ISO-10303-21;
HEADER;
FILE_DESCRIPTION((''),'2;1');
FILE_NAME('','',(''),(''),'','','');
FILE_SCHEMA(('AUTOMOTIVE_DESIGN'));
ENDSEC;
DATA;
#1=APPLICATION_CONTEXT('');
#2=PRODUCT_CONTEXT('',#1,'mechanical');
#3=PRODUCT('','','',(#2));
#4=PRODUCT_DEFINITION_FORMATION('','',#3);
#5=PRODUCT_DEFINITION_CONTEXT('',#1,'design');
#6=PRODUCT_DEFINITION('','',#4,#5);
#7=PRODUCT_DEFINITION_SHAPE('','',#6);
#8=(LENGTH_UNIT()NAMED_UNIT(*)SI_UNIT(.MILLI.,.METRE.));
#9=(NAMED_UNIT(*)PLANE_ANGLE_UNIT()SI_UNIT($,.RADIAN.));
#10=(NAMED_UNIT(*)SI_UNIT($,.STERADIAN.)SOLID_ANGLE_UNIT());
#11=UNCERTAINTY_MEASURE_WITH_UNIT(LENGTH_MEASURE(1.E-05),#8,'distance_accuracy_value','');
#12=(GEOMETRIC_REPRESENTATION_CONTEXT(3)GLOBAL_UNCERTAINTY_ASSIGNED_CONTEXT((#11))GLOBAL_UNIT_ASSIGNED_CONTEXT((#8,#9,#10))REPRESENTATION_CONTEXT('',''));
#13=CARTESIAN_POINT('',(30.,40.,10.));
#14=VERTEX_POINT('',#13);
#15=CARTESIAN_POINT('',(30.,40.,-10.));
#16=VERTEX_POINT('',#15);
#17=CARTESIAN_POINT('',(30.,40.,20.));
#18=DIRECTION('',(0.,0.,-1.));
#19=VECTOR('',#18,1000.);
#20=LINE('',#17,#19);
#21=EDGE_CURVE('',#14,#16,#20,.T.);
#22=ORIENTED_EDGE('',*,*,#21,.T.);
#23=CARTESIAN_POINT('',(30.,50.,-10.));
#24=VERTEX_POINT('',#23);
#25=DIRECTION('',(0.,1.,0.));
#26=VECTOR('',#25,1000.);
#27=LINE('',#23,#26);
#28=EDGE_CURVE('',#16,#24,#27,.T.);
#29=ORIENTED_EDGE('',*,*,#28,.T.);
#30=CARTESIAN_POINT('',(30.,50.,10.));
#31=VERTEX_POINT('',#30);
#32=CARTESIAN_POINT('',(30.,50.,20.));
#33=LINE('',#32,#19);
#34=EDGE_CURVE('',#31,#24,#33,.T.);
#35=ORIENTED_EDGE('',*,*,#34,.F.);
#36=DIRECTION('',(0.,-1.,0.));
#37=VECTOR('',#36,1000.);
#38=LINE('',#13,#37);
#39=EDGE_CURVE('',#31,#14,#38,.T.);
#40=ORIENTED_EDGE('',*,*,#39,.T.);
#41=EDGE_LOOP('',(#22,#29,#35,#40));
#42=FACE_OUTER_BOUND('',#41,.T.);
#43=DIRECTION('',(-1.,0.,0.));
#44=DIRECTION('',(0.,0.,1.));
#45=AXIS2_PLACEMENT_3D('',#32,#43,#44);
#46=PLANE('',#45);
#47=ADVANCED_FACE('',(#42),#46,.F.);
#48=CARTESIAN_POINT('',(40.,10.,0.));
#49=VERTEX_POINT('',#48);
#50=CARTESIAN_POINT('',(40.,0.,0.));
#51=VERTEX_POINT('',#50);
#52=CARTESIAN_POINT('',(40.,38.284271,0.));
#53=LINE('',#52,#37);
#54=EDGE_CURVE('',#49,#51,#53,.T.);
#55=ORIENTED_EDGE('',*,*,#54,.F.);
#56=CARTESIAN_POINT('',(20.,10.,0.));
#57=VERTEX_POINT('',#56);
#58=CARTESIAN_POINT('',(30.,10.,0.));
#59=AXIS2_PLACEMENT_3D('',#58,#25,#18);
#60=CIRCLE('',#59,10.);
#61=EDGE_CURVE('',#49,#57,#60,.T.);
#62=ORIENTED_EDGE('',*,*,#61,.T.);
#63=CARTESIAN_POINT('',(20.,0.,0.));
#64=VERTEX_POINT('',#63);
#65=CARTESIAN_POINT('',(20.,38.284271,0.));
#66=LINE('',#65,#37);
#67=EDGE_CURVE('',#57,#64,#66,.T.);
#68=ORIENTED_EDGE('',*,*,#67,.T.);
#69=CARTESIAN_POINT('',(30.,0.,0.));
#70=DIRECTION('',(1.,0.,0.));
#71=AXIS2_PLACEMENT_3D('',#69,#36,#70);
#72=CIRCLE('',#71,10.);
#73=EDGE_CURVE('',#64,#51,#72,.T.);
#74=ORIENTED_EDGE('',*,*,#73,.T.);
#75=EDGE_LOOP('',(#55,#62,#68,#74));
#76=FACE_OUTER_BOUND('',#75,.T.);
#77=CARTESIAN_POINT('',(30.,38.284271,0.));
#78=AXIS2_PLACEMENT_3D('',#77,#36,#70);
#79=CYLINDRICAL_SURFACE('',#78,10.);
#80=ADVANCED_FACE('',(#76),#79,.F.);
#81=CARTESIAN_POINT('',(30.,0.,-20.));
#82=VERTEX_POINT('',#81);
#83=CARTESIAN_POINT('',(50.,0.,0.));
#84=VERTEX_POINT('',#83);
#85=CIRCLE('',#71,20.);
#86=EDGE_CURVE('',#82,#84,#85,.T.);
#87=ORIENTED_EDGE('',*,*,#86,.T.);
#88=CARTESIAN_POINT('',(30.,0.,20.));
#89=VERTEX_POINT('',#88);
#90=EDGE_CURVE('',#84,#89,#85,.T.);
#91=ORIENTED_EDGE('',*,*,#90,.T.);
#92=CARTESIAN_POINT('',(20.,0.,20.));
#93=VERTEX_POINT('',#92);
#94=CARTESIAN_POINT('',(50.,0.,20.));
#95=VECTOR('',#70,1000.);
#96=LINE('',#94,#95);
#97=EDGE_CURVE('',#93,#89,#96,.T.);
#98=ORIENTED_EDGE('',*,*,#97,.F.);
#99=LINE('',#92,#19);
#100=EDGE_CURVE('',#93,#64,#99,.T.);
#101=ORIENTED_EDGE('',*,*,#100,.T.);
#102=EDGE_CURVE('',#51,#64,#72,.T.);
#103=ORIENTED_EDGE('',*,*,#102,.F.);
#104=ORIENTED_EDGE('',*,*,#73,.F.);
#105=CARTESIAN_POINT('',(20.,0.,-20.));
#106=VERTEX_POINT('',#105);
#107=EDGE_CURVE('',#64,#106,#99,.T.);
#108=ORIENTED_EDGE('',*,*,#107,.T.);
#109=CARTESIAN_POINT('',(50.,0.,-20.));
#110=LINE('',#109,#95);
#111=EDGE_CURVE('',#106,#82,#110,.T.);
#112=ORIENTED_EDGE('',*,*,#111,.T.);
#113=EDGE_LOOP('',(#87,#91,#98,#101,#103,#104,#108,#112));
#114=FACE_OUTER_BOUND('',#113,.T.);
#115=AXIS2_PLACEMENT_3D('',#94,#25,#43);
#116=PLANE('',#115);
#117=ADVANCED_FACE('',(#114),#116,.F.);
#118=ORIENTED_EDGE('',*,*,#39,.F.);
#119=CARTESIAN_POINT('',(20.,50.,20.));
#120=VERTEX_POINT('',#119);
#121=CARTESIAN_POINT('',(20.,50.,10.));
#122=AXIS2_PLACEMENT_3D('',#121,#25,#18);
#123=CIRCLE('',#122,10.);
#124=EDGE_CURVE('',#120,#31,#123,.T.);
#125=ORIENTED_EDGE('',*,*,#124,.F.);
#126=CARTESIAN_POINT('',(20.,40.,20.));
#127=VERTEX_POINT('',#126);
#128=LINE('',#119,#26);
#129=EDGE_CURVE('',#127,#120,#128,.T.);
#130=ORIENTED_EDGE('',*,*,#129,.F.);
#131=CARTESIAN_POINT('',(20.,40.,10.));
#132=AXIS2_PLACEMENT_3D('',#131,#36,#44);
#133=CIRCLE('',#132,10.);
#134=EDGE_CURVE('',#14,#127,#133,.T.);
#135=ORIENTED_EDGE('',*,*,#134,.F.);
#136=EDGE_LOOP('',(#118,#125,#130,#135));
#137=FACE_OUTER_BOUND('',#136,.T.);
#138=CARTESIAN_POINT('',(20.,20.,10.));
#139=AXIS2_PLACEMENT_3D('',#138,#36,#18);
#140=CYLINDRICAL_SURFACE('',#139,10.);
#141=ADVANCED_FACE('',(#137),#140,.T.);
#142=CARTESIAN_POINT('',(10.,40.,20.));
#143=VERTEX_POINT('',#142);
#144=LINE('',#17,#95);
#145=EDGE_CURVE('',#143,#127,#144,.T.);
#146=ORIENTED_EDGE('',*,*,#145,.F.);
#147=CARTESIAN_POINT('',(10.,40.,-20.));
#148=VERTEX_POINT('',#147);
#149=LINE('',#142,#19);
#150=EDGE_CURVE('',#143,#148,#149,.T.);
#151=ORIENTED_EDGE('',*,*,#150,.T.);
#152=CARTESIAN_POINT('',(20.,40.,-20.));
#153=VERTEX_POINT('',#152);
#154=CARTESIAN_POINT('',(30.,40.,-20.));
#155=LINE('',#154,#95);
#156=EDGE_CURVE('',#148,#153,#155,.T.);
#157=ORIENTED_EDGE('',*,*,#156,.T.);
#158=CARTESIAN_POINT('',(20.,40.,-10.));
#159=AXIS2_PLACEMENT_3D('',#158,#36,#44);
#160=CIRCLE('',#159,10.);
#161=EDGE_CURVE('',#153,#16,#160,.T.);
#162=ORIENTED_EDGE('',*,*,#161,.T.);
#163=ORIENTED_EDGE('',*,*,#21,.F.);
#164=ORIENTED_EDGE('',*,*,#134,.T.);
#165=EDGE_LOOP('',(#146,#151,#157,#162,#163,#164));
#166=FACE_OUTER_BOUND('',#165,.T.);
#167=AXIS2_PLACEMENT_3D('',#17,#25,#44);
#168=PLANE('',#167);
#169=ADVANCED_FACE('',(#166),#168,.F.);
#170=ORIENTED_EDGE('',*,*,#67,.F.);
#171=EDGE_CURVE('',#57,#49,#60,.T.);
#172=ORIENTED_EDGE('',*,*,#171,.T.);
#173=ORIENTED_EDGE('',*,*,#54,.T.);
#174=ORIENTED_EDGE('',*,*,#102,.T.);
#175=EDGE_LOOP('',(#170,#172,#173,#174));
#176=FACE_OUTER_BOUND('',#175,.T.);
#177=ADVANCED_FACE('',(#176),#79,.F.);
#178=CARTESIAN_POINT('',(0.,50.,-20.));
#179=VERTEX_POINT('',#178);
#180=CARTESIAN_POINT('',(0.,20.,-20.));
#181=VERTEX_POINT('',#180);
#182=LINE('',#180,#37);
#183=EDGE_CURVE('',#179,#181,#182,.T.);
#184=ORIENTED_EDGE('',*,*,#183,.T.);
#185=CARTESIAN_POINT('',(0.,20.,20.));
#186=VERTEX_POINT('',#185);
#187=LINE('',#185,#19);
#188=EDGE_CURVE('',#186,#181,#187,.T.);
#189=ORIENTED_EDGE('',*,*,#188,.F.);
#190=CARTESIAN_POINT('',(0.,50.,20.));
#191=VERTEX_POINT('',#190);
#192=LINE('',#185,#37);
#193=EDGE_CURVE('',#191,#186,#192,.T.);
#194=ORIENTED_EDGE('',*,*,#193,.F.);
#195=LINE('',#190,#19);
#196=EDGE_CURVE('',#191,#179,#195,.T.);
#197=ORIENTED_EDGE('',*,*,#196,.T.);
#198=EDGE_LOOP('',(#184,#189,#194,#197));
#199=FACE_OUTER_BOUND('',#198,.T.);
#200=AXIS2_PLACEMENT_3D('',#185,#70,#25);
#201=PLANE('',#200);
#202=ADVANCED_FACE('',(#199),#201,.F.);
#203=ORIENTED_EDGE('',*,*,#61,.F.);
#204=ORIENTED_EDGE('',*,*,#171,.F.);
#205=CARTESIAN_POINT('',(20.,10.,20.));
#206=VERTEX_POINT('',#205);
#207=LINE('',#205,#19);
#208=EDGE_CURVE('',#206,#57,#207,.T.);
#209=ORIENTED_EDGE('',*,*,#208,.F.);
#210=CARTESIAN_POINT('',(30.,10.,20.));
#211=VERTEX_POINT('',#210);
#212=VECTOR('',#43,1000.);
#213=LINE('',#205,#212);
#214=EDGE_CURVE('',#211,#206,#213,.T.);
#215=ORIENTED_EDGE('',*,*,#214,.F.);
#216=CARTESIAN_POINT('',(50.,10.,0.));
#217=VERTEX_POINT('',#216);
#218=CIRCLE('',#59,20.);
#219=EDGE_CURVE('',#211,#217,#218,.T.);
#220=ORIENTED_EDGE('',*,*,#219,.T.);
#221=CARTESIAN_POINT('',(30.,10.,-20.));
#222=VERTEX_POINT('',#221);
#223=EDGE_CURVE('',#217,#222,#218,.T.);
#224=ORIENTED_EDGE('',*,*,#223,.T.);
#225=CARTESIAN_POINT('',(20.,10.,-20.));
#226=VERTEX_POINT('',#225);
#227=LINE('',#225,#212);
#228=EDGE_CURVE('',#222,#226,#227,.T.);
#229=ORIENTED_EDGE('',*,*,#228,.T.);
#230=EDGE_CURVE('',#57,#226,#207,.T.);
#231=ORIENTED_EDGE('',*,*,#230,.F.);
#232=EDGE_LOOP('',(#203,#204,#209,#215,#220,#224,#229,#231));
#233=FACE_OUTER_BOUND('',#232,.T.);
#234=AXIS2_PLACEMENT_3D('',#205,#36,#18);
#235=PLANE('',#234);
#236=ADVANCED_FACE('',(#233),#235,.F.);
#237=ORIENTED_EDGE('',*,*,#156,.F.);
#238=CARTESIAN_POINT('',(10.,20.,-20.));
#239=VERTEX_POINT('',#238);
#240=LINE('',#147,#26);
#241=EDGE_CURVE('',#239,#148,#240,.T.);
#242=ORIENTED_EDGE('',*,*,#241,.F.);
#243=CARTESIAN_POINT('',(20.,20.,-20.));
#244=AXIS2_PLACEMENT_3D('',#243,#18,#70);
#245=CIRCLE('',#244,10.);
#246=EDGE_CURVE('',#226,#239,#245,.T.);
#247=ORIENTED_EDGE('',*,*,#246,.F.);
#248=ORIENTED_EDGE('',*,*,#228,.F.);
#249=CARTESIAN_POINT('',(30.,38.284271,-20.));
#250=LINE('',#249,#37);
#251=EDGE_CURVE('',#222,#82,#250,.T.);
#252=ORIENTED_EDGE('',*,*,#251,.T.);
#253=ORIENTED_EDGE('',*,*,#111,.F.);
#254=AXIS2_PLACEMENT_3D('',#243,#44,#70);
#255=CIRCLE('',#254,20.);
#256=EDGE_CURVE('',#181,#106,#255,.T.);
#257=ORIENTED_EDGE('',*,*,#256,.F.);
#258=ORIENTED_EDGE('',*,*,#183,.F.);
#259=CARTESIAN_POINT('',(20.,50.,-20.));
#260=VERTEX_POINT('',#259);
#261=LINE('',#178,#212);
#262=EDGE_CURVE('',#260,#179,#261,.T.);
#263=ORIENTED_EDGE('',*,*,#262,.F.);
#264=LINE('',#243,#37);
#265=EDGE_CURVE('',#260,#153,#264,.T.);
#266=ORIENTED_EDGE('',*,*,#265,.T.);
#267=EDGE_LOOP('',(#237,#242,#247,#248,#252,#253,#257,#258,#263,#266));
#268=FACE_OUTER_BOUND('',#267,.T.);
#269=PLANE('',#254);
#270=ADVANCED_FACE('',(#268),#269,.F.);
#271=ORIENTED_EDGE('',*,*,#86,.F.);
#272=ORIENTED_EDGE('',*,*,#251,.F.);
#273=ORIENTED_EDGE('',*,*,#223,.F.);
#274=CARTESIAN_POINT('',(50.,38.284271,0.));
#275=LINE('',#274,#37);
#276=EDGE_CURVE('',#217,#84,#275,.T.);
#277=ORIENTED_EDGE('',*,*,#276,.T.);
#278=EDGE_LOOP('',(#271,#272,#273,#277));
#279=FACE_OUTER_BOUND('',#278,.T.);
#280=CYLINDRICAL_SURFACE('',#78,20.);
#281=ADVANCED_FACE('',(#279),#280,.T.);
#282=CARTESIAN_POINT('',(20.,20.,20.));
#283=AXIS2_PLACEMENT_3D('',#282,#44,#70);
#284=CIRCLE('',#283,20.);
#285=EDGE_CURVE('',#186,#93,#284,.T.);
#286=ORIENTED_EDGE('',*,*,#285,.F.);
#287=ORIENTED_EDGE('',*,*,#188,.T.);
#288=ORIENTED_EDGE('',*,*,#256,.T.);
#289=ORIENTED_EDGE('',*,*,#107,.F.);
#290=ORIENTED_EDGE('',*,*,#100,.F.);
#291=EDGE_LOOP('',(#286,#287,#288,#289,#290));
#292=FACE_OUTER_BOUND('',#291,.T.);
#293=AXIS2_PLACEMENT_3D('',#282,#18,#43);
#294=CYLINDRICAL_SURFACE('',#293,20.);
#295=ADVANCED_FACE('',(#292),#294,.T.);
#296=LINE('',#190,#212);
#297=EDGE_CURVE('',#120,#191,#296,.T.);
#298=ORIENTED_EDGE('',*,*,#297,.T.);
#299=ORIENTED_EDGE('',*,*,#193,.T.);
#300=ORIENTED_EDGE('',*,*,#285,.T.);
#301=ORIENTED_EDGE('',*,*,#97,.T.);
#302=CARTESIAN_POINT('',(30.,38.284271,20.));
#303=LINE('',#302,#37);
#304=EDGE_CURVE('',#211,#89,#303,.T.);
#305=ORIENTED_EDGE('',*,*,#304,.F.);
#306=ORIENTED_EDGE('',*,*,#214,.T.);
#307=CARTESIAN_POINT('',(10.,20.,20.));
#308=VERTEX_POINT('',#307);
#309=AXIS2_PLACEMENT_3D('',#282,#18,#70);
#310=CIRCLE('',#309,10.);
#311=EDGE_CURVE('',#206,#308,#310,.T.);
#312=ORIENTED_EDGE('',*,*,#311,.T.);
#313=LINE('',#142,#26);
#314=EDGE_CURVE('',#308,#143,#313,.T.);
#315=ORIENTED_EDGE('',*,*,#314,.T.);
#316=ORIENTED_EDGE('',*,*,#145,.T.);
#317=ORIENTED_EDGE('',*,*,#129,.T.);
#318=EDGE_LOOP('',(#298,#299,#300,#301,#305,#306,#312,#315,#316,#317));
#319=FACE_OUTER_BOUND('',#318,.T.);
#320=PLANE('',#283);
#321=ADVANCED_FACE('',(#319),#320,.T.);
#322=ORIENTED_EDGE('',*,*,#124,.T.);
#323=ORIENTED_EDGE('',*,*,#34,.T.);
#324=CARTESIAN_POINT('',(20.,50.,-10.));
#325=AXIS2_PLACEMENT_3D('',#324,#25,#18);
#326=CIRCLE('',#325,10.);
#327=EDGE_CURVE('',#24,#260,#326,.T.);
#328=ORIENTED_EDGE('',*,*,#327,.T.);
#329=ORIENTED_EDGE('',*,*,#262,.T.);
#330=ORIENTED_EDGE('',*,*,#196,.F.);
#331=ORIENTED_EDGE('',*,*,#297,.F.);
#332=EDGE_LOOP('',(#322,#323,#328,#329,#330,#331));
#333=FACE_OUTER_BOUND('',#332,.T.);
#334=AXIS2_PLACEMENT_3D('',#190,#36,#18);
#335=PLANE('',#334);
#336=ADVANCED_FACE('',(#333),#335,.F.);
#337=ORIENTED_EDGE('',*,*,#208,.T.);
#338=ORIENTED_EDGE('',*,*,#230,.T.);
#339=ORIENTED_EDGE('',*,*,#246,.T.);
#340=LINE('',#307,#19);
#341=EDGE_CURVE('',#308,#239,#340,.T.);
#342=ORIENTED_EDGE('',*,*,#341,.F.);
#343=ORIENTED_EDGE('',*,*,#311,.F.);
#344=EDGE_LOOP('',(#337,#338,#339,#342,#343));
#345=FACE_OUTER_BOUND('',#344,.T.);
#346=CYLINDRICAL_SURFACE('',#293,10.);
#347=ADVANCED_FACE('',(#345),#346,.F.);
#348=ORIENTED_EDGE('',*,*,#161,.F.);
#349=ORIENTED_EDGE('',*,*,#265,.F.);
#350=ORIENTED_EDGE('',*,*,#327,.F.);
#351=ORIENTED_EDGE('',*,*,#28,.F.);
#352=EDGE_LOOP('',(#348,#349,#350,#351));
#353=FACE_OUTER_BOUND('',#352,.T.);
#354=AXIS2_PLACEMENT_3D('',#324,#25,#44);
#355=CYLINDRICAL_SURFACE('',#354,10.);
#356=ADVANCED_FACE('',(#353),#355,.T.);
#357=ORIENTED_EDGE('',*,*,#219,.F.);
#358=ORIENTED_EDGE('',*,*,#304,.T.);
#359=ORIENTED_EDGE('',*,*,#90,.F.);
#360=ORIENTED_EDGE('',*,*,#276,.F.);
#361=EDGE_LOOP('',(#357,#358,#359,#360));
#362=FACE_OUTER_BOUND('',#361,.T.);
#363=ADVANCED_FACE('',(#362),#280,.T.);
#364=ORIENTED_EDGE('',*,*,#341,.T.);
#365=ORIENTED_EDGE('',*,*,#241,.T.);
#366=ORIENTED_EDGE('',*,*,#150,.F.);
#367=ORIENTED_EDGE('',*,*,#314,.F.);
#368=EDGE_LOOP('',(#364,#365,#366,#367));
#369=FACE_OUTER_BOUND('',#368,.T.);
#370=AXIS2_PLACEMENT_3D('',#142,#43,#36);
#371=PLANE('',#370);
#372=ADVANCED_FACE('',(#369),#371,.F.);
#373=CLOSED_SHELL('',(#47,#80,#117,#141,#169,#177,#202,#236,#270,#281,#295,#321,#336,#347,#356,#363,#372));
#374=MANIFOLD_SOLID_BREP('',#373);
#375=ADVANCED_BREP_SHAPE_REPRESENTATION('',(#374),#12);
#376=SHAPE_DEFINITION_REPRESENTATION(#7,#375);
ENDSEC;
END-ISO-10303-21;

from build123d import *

# Parameters (mm, degrees)
BRACKET_BODY_DEPTH      = 20
EDGE_FILLETS_R10_R      = 10
MOUNTING_HOLE_SKETCH_R  = 10
MOUNTING_HOLE_CUT_DEPTH = 10


with BuildPart() as part:
    # Bracket Profile Sketch → Bracket Body (new, symmetric)
    with BuildSketch(Plane.XY):
        with BuildLine():
            Line((0, 20), (0, 50))
            Line((0, 50), (30, 50))
            Line((30, 50), (30, 40))
            Line((30, 40), (10, 40))
            Line((10, 40), (10, 20))
            ThreePointArc((10, 20), (12.928932188, 12.928932188), (20, 10))
            Line((20, 10), (50, 10))
            Line((50, 10), (50, 0))
            Line((50, 0), (20, 0))
            ThreePointArc((20, 0), (5.857864376, 5.857864376), (0, 20))
        make_face()
    extrude(amount=BRACKET_BODY_DEPTH, both=True)

    # Edge Fillets R10
    edge_fillets_r10_edges = [part.edges().sort_by_distance(p)[0] for p in [
        (30, 45, -20),
        (30, 45, 20),
    ]]
    fillet(edge_fillets_r10_edges, radius=EDGE_FILLETS_R10_R)

    # Mounting Hole Sketch → Mounting Hole Cut (cut)
    with BuildSketch(Plane.XZ):
        with BuildLine():
            Line((50, 20), (30, 20))
            ThreePointArc((30, 20), (44.142135624, 14.142135624), (50, 0))
            Line((50, 0), (50, 20))
        make_face()
        with BuildLine():
            Line((50, -20), (50, 0))
            ThreePointArc((50, 0), (44.142135624, -14.142135624), (30, -20))
            Line((30, -20), (50, -20))
        make_face()
        with Locations(Location((30, 0, 0), (0, 0, 180))):
            Circle(MOUNTING_HOLE_SKETCH_R)
    extrude(amount=-MOUNTING_HOLE_CUT_DEPTH, mode=Mode.SUBTRACT)


solid = part.part
